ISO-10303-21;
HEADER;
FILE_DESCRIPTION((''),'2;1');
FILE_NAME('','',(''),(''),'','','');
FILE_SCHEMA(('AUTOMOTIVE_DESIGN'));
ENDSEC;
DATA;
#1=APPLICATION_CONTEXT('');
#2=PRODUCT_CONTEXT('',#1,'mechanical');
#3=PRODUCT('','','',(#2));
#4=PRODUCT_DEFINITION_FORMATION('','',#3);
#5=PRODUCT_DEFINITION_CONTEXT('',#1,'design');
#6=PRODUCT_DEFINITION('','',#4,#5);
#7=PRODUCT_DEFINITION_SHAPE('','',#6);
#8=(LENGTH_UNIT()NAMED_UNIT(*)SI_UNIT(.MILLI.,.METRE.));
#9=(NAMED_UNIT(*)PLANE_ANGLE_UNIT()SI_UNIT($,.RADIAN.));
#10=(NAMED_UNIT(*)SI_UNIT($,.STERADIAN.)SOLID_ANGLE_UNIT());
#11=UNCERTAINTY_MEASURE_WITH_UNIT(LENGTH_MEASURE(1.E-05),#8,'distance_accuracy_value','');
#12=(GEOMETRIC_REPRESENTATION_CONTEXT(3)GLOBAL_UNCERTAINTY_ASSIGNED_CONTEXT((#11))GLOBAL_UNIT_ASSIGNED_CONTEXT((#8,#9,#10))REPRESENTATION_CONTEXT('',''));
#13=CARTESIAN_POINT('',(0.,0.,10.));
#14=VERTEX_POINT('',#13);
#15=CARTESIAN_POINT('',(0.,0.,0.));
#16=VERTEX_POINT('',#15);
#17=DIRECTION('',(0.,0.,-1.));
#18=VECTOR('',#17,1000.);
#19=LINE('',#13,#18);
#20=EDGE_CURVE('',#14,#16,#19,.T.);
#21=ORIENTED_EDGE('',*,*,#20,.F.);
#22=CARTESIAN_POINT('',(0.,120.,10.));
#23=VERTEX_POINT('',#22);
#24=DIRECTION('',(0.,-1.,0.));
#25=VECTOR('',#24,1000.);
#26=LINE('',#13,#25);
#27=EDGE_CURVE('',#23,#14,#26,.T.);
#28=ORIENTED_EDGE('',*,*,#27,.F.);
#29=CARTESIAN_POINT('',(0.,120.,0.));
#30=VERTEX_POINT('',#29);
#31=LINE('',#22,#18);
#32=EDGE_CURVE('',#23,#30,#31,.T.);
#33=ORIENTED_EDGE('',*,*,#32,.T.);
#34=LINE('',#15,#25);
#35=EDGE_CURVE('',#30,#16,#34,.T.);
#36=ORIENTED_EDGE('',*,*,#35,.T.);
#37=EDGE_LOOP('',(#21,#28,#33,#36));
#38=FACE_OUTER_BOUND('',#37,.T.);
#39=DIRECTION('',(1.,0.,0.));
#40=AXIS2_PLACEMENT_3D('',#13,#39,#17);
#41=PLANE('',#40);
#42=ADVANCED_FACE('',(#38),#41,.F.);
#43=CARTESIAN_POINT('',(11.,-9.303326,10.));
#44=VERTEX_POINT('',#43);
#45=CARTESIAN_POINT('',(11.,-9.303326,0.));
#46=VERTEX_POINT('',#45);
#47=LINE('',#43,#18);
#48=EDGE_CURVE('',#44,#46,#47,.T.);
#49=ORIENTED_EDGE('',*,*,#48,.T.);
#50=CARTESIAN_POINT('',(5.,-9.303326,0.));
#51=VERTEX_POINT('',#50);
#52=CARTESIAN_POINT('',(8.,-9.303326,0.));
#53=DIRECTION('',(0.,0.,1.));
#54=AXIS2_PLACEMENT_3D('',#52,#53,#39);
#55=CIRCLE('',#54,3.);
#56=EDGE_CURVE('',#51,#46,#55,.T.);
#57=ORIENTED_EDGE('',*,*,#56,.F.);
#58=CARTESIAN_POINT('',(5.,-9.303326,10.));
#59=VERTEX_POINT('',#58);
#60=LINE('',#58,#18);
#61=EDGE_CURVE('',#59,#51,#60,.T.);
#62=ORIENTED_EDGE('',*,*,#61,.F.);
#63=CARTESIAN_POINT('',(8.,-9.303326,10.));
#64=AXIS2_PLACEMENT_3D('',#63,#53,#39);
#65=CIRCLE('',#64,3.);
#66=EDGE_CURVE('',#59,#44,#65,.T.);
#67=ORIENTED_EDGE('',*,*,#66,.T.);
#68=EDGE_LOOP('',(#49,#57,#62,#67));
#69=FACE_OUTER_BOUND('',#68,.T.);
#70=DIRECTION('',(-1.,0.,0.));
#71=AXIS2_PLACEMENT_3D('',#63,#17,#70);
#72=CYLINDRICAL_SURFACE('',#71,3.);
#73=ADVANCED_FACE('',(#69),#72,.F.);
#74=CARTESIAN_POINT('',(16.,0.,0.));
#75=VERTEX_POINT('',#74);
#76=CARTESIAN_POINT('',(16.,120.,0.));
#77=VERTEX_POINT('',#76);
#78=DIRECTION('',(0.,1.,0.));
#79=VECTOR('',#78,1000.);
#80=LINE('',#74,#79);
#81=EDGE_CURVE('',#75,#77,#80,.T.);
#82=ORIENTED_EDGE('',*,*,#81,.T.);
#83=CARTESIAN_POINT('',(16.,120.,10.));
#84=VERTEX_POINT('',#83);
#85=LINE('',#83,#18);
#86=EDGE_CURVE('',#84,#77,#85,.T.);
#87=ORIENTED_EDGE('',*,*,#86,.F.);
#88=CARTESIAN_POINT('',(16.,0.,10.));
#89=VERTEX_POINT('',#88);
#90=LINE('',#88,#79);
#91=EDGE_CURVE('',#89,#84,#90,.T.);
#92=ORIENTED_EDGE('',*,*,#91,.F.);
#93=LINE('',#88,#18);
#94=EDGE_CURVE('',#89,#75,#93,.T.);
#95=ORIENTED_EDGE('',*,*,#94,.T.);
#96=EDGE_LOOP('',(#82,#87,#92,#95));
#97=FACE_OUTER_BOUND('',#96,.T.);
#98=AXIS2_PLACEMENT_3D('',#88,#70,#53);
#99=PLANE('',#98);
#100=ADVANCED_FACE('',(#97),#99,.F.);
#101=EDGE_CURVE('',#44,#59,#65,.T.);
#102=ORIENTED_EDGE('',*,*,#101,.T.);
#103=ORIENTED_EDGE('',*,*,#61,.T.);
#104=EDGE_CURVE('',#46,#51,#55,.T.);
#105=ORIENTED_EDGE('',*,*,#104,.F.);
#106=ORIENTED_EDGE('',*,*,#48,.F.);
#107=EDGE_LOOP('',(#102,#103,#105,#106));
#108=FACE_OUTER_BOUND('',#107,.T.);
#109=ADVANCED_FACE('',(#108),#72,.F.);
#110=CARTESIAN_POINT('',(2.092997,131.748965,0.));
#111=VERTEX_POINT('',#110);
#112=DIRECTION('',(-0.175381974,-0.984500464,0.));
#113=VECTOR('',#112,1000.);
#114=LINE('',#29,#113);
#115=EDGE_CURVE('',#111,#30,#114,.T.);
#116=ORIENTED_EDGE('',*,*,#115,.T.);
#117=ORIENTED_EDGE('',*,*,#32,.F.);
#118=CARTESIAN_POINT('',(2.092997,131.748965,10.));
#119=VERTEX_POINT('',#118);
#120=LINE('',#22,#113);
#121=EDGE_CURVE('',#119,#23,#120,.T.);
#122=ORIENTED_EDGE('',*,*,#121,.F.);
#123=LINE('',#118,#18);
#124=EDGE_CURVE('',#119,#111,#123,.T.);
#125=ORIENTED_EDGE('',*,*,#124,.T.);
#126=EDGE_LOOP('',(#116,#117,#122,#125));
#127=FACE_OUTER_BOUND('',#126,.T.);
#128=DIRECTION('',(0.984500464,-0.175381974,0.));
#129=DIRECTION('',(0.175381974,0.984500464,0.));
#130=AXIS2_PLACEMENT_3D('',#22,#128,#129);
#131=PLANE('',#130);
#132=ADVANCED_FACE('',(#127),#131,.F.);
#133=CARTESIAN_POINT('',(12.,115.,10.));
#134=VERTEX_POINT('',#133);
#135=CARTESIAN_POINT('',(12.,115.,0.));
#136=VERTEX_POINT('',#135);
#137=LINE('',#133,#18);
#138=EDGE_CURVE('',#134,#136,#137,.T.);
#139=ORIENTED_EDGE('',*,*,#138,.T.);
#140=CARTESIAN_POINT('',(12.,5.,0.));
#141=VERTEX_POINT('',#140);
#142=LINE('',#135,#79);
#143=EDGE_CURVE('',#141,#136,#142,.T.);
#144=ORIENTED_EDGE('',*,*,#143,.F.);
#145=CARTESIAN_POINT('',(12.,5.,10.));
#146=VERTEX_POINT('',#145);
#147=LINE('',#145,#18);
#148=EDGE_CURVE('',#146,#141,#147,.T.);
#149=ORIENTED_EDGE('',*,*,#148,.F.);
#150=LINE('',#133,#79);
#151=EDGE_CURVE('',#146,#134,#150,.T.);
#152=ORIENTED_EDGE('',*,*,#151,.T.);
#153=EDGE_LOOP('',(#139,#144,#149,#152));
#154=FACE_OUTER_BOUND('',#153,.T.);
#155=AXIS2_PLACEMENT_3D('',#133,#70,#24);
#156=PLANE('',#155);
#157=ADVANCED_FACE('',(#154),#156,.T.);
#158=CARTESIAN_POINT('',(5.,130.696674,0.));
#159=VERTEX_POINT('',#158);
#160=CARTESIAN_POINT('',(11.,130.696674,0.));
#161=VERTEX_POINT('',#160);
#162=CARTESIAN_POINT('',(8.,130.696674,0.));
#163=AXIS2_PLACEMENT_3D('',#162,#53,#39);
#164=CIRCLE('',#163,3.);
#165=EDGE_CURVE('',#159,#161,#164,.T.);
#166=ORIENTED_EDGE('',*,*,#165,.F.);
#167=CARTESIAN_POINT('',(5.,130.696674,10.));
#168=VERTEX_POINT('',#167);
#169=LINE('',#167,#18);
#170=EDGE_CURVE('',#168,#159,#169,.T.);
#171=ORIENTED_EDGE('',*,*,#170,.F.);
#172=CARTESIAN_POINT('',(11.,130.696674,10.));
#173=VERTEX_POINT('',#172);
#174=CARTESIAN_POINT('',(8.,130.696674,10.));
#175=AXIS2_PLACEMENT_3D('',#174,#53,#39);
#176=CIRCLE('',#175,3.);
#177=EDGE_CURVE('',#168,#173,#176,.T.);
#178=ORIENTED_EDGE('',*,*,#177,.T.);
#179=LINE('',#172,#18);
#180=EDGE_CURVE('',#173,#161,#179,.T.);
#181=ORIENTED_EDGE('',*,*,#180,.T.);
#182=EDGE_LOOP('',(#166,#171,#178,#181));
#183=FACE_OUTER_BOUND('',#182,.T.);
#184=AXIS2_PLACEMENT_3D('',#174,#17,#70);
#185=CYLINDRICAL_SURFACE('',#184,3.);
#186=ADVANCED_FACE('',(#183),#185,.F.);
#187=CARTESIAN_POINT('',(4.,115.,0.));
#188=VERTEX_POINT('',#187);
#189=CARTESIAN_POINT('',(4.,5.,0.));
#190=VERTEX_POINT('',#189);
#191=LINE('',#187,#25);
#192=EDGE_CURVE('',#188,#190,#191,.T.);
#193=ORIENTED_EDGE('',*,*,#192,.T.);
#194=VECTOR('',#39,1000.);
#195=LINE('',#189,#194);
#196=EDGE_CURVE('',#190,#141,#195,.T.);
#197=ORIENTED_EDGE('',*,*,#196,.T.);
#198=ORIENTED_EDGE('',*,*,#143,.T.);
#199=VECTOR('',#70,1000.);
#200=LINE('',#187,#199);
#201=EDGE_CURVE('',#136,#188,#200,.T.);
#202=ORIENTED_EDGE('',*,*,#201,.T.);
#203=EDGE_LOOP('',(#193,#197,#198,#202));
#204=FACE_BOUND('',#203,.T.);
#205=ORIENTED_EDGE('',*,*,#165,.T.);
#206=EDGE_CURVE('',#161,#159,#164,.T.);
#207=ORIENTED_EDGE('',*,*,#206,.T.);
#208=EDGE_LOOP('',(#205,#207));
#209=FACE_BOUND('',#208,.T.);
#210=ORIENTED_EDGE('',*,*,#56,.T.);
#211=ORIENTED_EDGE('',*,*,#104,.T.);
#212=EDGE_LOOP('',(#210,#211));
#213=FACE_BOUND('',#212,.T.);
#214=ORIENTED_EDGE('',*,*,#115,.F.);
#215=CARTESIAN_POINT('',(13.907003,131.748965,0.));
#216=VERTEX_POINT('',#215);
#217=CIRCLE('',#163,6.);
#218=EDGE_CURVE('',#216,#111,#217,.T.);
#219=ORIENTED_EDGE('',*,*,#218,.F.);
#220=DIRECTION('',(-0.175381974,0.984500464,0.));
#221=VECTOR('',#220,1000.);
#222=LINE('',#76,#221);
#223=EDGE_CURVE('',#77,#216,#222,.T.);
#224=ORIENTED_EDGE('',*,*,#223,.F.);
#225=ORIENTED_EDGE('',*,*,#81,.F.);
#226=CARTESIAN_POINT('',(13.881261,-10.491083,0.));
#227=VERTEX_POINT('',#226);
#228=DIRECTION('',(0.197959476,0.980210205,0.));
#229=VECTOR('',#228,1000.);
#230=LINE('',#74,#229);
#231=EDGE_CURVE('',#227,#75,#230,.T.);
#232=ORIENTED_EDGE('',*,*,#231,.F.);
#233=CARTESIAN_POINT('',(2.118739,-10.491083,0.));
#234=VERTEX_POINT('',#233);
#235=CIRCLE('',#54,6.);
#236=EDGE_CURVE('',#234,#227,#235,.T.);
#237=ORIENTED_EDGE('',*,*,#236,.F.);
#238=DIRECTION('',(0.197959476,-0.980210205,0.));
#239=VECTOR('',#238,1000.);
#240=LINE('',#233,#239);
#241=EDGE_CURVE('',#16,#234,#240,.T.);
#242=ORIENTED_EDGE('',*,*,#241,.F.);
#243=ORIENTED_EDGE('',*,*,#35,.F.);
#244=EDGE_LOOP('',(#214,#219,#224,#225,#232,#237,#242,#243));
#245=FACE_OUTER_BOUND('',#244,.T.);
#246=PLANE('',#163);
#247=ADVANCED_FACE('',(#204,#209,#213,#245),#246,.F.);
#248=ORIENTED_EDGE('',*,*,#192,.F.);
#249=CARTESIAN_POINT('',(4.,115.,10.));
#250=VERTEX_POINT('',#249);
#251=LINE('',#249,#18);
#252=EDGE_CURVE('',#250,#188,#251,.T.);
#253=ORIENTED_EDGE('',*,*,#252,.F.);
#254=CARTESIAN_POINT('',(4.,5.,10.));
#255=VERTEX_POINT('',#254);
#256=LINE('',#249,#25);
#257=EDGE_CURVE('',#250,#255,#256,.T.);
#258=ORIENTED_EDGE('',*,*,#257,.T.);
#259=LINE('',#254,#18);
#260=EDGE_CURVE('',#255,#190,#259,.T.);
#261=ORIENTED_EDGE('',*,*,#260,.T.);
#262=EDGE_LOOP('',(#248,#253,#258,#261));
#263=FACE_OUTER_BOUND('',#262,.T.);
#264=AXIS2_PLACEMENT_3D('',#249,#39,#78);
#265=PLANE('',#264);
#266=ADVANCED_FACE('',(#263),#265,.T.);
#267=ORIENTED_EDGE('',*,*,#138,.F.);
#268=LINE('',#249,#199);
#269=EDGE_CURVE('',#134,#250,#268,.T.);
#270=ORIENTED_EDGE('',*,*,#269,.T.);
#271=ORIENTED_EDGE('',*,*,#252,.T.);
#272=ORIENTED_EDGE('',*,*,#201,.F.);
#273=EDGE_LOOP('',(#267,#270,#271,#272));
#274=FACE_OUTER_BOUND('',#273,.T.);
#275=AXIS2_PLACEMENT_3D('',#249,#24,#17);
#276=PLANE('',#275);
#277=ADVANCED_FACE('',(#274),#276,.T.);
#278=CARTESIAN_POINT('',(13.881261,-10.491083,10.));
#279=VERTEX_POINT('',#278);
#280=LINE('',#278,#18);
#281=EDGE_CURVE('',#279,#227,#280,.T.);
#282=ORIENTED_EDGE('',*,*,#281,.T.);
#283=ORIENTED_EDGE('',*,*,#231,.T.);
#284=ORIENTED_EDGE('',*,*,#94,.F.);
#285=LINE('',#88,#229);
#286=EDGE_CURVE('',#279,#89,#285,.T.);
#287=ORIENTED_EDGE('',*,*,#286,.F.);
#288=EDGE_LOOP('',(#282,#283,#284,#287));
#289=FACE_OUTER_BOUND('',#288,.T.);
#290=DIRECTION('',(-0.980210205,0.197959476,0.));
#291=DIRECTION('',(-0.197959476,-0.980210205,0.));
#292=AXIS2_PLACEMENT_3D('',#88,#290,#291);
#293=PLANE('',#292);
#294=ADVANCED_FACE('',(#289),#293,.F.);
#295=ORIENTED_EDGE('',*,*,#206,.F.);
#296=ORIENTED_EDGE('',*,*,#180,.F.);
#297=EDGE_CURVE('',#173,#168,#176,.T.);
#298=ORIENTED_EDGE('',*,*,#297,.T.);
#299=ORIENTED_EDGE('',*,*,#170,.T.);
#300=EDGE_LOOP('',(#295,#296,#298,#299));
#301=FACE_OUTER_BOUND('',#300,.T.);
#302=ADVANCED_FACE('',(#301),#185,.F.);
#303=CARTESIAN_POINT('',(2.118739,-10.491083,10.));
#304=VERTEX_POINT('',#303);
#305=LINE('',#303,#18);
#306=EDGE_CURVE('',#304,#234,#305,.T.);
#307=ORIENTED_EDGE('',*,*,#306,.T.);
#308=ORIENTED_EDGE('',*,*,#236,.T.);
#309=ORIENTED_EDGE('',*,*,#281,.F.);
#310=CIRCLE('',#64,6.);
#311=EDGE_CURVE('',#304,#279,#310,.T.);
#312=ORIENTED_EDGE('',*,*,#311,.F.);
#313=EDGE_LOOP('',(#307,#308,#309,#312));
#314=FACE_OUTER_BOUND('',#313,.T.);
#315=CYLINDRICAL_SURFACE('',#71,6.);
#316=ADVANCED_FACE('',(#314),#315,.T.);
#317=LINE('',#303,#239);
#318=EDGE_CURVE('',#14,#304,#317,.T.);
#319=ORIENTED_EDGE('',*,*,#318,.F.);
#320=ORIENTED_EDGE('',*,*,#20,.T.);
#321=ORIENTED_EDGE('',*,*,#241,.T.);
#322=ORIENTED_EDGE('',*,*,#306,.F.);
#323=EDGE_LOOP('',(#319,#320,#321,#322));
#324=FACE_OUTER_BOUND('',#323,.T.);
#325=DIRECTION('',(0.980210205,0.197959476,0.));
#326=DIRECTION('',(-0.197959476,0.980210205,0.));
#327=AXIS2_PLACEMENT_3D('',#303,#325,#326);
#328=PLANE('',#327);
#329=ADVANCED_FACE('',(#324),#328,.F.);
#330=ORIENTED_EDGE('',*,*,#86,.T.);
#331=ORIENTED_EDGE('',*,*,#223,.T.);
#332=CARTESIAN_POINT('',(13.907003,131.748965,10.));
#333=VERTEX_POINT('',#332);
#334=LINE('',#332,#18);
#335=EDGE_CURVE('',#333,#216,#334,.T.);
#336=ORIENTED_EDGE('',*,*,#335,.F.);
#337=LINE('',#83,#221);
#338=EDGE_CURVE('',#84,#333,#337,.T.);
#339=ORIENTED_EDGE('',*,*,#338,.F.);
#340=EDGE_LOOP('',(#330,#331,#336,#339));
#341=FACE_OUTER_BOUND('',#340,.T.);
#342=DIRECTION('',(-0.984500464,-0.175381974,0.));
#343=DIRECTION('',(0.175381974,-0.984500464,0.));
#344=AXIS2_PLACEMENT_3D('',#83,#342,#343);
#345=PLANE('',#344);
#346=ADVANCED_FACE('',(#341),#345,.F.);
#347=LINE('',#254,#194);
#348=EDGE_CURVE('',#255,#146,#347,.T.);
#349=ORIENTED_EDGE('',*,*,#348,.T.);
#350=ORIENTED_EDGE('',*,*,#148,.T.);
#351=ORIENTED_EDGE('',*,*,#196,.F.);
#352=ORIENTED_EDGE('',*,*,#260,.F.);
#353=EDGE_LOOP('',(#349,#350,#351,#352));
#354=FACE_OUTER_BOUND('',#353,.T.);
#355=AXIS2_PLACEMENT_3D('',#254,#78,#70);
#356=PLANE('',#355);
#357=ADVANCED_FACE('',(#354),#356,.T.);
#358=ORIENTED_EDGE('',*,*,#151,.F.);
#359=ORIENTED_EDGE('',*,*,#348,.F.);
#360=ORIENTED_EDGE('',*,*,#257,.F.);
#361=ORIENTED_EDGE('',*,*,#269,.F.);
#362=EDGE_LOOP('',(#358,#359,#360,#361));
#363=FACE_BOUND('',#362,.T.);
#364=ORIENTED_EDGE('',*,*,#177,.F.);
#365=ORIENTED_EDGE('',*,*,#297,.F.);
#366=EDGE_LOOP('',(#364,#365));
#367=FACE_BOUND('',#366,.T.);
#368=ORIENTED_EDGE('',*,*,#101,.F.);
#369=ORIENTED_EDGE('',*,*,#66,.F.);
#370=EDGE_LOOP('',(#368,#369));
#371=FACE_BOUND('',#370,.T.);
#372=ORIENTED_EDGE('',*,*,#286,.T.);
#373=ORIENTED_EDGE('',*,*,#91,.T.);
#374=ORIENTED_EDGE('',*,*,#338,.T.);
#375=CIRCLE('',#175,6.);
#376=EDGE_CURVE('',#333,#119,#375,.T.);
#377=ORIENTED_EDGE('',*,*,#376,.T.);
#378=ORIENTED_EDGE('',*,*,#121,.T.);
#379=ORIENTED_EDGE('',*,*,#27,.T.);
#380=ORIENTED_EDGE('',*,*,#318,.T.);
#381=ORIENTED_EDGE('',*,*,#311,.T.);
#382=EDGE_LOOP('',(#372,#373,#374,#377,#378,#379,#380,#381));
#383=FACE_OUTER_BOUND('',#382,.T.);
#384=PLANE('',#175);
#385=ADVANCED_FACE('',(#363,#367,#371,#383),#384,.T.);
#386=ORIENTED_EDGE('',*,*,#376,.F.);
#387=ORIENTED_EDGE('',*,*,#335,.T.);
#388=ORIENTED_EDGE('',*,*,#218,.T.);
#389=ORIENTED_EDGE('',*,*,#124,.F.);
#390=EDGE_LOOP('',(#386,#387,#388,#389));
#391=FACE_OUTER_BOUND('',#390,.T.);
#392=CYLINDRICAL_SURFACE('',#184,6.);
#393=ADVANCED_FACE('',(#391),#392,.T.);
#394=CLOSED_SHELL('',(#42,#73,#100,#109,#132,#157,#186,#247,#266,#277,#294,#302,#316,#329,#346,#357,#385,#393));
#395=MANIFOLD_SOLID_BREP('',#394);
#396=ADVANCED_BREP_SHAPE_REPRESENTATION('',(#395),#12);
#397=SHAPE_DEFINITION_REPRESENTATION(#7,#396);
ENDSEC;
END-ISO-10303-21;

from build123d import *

# Parameters (mm, degrees)
SKETCH1_R           = 3
SKETCH1_W           = 8
SKETCH1_H           = 110
BOSS_EXTRUDE1_DEPTH = 10


with BuildPart() as part:
    # Sketch1 → Boss-Extrude1 (new body)
    with BuildSketch(Plane.XY):
        with BuildLine():
            Line((2.118738771, -10.491083349), (0, 0))
            Line((0, 0), (0, 120))
            Line((0, 120), (2.092997217, 131.74896535))
            ThreePointArc((2.092997217, 131.74896535), (8, 136.696673509), (13.907002783, 131.74896535))
            Line((13.907002783, 131.74896535), (16, 120))
            Line((16, 120), (16, 0))
            Line((16, 0), (13.881261229, -10.491083349))
            ThreePointArc((13.881261229, -10.491083349), (8, -15.303326491), (2.118738771, -10.491083349))
        make_face()
        with Locations((8, 130.696673509)):
            Circle(SKETCH1_R, mode=Mode.SUBTRACT)
        with Locations((8, -9.303326491)):
            Circle(SKETCH1_R, mode=Mode.SUBTRACT)
        with Locations((8, 60)):
            Rectangle(SKETCH1_W, SKETCH1_H, mode=Mode.SUBTRACT)
    extrude(amount=BOSS_EXTRUDE1_DEPTH)


solid = part.part
